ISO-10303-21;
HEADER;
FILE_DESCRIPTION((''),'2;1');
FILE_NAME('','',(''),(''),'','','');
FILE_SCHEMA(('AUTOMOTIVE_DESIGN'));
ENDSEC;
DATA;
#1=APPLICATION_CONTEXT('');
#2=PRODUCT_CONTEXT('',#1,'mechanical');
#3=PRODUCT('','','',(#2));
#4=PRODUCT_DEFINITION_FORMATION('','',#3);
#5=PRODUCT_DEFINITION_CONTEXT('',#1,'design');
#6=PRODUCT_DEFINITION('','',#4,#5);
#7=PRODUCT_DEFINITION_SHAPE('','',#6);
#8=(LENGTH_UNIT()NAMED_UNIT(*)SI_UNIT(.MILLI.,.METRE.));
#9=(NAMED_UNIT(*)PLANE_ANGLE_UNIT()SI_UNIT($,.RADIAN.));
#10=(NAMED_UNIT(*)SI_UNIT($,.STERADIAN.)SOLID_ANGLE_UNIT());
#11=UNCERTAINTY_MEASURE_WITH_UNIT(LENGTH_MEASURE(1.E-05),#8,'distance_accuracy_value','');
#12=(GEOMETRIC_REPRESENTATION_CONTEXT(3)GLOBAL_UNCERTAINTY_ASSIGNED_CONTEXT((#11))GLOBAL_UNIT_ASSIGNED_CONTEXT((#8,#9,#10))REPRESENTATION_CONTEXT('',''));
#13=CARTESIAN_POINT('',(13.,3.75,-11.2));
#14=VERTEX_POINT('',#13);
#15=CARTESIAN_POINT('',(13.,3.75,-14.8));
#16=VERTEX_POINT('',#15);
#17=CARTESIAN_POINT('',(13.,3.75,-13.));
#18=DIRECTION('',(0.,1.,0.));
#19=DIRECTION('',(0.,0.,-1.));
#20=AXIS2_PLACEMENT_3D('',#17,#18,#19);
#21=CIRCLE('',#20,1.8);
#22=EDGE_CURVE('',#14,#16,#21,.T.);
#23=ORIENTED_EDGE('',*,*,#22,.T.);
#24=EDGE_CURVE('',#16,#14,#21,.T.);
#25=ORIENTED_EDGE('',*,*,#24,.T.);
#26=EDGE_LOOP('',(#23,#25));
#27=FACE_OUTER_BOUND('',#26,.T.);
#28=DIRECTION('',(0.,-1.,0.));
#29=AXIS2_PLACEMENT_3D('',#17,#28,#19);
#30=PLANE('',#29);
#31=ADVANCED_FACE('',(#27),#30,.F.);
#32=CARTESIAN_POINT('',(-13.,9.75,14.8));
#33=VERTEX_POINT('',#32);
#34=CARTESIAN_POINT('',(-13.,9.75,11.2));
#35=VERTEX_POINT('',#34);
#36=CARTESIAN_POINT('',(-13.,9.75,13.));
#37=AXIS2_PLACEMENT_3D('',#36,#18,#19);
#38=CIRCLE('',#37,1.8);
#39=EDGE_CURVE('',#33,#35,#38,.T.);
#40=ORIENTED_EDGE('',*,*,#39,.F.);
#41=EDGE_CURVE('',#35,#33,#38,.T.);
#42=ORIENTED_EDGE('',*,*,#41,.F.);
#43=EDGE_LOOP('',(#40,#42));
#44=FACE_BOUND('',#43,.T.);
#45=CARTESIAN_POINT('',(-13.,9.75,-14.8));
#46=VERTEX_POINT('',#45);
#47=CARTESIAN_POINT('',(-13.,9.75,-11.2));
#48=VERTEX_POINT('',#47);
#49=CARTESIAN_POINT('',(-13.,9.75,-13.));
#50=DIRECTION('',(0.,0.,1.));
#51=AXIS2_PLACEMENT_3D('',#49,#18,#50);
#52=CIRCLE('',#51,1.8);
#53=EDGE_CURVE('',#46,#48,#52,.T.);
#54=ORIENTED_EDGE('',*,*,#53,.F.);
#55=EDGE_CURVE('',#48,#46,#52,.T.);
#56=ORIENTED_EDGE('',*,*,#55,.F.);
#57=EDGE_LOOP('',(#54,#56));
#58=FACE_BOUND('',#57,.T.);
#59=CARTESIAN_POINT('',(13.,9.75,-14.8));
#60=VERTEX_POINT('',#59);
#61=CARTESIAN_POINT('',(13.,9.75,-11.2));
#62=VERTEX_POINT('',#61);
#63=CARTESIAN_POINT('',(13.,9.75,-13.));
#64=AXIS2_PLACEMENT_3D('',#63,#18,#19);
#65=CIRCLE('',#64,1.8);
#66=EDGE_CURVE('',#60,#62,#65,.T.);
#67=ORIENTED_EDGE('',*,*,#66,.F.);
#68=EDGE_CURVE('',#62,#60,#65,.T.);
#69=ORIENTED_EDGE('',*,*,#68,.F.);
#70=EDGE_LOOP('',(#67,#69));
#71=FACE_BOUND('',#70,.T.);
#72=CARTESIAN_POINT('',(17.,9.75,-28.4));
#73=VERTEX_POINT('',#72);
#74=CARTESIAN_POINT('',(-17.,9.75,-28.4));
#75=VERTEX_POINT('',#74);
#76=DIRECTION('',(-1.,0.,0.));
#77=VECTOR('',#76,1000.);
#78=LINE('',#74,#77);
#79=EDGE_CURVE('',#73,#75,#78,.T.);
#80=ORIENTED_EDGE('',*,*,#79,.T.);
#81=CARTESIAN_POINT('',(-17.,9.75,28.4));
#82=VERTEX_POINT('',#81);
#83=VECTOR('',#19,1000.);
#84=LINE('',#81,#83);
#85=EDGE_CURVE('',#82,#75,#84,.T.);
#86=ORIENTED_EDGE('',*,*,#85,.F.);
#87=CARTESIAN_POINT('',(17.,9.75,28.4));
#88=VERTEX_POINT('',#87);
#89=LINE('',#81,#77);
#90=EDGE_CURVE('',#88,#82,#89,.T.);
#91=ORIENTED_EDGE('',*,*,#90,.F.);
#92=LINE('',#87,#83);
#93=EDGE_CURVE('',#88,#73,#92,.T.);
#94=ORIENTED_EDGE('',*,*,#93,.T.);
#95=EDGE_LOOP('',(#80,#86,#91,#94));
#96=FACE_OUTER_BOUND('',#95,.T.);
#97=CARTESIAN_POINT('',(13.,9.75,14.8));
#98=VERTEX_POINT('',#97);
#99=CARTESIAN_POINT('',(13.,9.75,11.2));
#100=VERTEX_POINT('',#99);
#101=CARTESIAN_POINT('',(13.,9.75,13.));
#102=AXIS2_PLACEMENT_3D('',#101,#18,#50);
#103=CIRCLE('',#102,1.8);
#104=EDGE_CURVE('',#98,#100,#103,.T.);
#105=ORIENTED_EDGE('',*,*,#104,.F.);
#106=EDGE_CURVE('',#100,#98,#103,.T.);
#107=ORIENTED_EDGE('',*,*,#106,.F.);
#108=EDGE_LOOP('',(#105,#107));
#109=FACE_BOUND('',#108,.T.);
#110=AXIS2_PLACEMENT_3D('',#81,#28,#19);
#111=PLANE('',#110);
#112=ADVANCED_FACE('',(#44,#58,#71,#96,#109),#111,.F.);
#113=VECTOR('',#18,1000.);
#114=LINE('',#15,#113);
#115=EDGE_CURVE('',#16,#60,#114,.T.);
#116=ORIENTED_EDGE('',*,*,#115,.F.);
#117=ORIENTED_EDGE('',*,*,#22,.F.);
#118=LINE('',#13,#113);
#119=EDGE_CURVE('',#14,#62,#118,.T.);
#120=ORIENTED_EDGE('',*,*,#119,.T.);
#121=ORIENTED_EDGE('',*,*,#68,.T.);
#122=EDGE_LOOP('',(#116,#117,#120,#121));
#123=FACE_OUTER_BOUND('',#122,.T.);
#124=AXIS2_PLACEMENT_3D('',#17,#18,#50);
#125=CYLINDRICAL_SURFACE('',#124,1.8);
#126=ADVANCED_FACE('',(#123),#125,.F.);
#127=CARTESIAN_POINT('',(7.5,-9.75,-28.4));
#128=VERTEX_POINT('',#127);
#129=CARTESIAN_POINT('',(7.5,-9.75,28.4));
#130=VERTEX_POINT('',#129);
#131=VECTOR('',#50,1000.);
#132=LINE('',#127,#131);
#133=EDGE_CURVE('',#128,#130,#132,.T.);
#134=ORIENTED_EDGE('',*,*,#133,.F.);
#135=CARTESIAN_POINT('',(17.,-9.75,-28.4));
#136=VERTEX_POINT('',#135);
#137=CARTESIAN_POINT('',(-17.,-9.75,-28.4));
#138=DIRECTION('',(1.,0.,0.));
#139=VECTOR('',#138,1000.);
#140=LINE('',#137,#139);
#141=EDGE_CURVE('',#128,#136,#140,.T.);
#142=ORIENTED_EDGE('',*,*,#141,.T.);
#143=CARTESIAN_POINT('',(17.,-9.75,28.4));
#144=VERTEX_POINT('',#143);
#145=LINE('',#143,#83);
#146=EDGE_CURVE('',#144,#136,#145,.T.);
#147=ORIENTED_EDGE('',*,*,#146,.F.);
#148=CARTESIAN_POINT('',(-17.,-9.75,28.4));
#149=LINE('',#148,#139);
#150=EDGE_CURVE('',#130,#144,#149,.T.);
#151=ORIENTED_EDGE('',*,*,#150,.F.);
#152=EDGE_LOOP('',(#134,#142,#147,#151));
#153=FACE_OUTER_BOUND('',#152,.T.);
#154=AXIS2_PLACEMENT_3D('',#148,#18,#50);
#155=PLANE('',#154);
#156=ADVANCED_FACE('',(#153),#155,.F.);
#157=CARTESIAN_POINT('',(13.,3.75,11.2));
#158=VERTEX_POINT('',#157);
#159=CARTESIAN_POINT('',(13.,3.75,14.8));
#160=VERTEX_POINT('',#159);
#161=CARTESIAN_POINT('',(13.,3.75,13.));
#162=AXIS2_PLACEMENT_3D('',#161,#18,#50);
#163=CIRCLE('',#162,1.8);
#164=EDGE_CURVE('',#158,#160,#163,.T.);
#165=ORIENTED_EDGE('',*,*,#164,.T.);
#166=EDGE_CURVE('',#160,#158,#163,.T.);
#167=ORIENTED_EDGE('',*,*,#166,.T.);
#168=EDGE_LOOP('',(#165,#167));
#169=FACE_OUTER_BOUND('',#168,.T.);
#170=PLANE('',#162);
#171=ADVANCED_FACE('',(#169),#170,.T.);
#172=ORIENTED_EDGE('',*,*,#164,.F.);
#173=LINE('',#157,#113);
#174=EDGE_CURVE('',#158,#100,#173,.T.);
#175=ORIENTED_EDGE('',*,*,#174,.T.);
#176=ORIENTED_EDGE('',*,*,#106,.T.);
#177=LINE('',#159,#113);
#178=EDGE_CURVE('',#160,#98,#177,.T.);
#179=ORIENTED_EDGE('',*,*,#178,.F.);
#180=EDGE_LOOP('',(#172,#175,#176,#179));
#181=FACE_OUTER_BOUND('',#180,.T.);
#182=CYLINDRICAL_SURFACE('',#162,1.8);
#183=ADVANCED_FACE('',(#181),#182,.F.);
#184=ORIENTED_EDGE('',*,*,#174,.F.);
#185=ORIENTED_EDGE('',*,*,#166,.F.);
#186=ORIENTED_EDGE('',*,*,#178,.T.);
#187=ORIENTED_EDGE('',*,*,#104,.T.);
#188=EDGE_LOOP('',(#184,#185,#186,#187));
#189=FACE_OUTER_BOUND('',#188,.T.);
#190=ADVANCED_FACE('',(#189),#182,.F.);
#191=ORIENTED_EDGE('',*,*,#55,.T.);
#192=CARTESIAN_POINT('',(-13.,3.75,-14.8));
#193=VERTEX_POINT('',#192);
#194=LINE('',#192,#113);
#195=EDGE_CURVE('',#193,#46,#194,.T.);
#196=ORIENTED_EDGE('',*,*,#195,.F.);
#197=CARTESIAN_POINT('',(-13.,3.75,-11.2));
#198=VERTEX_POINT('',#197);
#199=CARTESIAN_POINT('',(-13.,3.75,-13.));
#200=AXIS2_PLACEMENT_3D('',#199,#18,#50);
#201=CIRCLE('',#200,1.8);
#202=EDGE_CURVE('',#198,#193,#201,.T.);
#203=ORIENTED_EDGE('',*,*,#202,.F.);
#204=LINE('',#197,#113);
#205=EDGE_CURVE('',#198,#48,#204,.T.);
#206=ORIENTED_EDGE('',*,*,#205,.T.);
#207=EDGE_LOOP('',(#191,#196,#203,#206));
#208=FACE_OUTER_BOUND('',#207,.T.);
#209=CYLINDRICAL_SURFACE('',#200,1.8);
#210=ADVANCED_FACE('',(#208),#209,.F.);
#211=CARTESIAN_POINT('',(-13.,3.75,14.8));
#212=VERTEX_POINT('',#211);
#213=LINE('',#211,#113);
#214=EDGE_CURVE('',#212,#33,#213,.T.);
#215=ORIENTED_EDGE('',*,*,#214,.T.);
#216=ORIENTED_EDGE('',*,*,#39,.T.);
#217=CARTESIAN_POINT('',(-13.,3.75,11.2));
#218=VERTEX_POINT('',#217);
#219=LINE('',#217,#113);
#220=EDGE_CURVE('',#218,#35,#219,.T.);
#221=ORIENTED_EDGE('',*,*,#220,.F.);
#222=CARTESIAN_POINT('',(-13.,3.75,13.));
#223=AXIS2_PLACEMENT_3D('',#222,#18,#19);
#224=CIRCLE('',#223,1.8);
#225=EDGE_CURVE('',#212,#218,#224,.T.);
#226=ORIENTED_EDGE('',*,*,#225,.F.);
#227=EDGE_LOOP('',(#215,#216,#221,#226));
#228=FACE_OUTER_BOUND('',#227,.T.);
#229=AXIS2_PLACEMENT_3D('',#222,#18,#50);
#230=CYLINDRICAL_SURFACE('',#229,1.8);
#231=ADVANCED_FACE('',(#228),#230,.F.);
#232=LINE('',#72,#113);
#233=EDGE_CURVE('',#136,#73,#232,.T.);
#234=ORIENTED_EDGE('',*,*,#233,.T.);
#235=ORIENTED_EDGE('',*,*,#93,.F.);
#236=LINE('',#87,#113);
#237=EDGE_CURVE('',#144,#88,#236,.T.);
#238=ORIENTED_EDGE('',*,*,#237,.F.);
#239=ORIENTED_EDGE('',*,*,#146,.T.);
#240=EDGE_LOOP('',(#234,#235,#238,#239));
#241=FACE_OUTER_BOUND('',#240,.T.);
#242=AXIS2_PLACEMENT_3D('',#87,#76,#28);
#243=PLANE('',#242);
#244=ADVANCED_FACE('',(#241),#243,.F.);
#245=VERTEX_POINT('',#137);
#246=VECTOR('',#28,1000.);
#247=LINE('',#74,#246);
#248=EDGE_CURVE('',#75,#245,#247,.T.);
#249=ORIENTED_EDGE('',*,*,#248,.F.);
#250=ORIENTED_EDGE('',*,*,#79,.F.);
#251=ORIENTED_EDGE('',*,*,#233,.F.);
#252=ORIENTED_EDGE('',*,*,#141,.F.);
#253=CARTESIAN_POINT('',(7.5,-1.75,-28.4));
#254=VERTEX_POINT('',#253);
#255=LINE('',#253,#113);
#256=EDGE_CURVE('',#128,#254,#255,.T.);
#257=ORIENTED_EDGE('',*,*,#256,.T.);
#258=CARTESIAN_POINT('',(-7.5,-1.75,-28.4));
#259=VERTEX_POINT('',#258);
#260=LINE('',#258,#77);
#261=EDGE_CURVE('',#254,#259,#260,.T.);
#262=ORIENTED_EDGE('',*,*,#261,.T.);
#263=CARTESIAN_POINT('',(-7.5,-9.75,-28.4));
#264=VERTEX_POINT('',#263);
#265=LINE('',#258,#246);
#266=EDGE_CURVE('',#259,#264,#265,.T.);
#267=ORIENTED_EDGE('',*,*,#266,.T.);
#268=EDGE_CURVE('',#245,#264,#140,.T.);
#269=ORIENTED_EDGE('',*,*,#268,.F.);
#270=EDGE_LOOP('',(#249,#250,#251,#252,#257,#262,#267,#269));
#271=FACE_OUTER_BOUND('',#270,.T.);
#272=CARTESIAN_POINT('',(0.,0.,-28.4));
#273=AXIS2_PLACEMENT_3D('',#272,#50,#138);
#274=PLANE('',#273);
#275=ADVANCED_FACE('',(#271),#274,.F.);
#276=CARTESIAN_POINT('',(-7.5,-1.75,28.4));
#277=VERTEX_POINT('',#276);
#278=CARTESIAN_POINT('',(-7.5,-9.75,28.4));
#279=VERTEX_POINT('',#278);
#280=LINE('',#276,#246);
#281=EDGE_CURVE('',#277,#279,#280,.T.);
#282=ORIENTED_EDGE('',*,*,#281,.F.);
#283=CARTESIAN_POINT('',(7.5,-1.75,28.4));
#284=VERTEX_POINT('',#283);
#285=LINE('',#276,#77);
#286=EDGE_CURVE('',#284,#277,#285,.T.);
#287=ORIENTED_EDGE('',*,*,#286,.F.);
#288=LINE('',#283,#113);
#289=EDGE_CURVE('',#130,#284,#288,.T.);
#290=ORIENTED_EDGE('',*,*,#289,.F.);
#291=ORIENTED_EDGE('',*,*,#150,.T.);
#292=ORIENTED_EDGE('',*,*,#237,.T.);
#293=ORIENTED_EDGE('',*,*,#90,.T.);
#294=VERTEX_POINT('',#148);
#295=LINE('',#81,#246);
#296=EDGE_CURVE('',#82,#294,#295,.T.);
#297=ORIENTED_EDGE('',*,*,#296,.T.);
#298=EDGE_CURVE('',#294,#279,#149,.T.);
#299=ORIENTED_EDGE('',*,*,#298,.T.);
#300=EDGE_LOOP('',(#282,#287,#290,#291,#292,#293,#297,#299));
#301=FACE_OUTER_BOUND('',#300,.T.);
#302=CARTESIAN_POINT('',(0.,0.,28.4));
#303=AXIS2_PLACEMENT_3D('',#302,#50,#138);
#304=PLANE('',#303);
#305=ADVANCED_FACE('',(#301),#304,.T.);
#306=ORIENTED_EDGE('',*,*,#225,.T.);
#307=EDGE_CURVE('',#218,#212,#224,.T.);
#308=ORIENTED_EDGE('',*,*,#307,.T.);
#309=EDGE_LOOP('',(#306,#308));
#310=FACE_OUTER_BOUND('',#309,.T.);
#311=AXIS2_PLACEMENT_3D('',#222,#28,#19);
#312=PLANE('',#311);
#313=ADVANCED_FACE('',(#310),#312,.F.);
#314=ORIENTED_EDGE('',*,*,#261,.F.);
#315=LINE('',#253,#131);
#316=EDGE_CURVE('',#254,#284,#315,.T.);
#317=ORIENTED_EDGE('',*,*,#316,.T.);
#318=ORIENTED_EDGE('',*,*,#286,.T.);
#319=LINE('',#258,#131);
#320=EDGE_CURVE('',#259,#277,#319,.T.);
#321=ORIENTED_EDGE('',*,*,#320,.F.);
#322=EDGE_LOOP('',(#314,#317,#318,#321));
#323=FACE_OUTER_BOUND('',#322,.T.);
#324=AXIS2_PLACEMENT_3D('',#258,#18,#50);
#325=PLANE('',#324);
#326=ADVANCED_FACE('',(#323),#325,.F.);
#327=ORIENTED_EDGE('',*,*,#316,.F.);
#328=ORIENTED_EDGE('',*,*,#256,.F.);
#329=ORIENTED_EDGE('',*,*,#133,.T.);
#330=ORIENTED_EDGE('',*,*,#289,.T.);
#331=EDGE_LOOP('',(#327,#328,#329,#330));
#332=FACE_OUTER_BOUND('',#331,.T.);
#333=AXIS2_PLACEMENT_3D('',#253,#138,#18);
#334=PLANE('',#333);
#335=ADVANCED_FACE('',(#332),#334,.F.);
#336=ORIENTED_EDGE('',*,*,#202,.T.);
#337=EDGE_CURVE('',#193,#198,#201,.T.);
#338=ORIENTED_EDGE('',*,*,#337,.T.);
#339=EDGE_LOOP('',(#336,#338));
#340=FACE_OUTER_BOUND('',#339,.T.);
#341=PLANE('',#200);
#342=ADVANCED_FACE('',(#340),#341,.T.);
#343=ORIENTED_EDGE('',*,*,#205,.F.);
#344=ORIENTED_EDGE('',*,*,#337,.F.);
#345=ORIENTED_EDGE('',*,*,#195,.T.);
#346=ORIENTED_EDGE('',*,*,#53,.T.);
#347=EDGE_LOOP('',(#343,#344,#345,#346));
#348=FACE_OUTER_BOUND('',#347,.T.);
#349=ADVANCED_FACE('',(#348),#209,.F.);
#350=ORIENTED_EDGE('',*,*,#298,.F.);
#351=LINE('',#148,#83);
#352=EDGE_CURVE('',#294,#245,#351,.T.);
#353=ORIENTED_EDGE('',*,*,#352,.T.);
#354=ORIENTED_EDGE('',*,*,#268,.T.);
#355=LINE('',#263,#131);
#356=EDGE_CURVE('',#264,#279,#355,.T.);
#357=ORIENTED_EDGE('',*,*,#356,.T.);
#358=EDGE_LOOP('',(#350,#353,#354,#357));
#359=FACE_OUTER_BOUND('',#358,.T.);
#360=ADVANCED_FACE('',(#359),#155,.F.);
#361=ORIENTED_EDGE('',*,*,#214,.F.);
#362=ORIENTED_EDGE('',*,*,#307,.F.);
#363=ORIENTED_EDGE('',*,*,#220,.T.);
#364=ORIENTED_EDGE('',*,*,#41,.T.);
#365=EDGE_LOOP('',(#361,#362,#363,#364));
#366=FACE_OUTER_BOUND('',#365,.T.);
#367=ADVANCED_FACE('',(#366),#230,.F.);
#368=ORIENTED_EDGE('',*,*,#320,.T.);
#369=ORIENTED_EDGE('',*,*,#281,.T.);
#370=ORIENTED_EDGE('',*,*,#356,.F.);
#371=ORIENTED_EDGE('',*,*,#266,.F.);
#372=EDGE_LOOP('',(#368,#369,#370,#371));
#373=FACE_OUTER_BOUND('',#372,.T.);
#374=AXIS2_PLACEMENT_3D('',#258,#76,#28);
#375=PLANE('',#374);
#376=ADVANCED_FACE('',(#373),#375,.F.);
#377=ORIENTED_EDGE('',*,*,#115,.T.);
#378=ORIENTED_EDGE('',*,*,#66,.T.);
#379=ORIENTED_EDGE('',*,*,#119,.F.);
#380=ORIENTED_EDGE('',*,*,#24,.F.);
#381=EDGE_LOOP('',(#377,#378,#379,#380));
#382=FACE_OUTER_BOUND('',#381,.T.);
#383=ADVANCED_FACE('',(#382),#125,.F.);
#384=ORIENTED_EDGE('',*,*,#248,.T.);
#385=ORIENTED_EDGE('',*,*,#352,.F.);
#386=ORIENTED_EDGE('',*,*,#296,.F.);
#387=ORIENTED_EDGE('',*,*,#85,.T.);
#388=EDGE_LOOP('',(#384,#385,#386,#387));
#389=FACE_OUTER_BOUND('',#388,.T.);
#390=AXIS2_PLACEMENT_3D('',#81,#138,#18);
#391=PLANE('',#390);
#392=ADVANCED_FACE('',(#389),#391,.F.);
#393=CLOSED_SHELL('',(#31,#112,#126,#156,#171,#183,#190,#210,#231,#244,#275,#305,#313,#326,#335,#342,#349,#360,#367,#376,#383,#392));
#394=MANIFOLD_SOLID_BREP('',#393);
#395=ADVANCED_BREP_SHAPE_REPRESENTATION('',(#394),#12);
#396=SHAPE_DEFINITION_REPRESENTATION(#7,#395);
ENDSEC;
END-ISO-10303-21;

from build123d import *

# Parameters (mm, degrees)
SKETCH_1_W               = 34
SKETCH_1_H               = 19.5
EXTRUDE_1_DEPTH          = 28.4
CUT_EXTRUDE_1_DEPTH      = 35.505398128
CUT_EXTRUDE_1_DEPTH_BACK = 35.505398128
SKETCH_2_W               = 15
SKETCH_2_H               = 8
SKETCH_4_R               = 1.8
CUT_EXTRUDE_2_DEPTH      = 6


with BuildPart() as part:
    # 草图1 → 凸台-拉伸1 (new, symmetric)
    with BuildSketch(Plane.XY):
        Rectangle(SKETCH_1_W, SKETCH_1_H)
    extrude(amount=EXTRUDE_1_DEPTH, both=True)

    # 草图2 → 切除-拉伸1 (cut, two sides: drawn at the far end of the back side and taken through both)
    with BuildSketch(Plane.XY.offset(-CUT_EXTRUDE_1_DEPTH_BACK)):
        with Locations((0, -5.75)):
            Rectangle(SKETCH_2_W, SKETCH_2_H)
    extrude(amount=CUT_EXTRUDE_1_DEPTH + CUT_EXTRUDE_1_DEPTH_BACK, mode=Mode.SUBTRACT)

    # 草图4 → 切除-拉伸2 (cut)
    with BuildSketch(Plane(origin=(0, 9.75, 0), x_dir=(1, 0, 0), z_dir=(0, 1, 0))):
        with Locations(Location((-13, 13, 0), (0, 0, 270))):
            Circle(SKETCH_4_R)
        with Locations(Location((13, 13, 0), (0, 0, 90))):
            Circle(SKETCH_4_R)
        with Locations(Location((13, -13, 0), (0, 0, 270))):
            Circle(SKETCH_4_R)
        with Locations(Location((-13, -13, 0), (0, 0, 90))):
            Circle(SKETCH_4_R)
    extrude(amount=-CUT_EXTRUDE_2_DEPTH, mode=Mode.SUBTRACT)


solid = part.part
